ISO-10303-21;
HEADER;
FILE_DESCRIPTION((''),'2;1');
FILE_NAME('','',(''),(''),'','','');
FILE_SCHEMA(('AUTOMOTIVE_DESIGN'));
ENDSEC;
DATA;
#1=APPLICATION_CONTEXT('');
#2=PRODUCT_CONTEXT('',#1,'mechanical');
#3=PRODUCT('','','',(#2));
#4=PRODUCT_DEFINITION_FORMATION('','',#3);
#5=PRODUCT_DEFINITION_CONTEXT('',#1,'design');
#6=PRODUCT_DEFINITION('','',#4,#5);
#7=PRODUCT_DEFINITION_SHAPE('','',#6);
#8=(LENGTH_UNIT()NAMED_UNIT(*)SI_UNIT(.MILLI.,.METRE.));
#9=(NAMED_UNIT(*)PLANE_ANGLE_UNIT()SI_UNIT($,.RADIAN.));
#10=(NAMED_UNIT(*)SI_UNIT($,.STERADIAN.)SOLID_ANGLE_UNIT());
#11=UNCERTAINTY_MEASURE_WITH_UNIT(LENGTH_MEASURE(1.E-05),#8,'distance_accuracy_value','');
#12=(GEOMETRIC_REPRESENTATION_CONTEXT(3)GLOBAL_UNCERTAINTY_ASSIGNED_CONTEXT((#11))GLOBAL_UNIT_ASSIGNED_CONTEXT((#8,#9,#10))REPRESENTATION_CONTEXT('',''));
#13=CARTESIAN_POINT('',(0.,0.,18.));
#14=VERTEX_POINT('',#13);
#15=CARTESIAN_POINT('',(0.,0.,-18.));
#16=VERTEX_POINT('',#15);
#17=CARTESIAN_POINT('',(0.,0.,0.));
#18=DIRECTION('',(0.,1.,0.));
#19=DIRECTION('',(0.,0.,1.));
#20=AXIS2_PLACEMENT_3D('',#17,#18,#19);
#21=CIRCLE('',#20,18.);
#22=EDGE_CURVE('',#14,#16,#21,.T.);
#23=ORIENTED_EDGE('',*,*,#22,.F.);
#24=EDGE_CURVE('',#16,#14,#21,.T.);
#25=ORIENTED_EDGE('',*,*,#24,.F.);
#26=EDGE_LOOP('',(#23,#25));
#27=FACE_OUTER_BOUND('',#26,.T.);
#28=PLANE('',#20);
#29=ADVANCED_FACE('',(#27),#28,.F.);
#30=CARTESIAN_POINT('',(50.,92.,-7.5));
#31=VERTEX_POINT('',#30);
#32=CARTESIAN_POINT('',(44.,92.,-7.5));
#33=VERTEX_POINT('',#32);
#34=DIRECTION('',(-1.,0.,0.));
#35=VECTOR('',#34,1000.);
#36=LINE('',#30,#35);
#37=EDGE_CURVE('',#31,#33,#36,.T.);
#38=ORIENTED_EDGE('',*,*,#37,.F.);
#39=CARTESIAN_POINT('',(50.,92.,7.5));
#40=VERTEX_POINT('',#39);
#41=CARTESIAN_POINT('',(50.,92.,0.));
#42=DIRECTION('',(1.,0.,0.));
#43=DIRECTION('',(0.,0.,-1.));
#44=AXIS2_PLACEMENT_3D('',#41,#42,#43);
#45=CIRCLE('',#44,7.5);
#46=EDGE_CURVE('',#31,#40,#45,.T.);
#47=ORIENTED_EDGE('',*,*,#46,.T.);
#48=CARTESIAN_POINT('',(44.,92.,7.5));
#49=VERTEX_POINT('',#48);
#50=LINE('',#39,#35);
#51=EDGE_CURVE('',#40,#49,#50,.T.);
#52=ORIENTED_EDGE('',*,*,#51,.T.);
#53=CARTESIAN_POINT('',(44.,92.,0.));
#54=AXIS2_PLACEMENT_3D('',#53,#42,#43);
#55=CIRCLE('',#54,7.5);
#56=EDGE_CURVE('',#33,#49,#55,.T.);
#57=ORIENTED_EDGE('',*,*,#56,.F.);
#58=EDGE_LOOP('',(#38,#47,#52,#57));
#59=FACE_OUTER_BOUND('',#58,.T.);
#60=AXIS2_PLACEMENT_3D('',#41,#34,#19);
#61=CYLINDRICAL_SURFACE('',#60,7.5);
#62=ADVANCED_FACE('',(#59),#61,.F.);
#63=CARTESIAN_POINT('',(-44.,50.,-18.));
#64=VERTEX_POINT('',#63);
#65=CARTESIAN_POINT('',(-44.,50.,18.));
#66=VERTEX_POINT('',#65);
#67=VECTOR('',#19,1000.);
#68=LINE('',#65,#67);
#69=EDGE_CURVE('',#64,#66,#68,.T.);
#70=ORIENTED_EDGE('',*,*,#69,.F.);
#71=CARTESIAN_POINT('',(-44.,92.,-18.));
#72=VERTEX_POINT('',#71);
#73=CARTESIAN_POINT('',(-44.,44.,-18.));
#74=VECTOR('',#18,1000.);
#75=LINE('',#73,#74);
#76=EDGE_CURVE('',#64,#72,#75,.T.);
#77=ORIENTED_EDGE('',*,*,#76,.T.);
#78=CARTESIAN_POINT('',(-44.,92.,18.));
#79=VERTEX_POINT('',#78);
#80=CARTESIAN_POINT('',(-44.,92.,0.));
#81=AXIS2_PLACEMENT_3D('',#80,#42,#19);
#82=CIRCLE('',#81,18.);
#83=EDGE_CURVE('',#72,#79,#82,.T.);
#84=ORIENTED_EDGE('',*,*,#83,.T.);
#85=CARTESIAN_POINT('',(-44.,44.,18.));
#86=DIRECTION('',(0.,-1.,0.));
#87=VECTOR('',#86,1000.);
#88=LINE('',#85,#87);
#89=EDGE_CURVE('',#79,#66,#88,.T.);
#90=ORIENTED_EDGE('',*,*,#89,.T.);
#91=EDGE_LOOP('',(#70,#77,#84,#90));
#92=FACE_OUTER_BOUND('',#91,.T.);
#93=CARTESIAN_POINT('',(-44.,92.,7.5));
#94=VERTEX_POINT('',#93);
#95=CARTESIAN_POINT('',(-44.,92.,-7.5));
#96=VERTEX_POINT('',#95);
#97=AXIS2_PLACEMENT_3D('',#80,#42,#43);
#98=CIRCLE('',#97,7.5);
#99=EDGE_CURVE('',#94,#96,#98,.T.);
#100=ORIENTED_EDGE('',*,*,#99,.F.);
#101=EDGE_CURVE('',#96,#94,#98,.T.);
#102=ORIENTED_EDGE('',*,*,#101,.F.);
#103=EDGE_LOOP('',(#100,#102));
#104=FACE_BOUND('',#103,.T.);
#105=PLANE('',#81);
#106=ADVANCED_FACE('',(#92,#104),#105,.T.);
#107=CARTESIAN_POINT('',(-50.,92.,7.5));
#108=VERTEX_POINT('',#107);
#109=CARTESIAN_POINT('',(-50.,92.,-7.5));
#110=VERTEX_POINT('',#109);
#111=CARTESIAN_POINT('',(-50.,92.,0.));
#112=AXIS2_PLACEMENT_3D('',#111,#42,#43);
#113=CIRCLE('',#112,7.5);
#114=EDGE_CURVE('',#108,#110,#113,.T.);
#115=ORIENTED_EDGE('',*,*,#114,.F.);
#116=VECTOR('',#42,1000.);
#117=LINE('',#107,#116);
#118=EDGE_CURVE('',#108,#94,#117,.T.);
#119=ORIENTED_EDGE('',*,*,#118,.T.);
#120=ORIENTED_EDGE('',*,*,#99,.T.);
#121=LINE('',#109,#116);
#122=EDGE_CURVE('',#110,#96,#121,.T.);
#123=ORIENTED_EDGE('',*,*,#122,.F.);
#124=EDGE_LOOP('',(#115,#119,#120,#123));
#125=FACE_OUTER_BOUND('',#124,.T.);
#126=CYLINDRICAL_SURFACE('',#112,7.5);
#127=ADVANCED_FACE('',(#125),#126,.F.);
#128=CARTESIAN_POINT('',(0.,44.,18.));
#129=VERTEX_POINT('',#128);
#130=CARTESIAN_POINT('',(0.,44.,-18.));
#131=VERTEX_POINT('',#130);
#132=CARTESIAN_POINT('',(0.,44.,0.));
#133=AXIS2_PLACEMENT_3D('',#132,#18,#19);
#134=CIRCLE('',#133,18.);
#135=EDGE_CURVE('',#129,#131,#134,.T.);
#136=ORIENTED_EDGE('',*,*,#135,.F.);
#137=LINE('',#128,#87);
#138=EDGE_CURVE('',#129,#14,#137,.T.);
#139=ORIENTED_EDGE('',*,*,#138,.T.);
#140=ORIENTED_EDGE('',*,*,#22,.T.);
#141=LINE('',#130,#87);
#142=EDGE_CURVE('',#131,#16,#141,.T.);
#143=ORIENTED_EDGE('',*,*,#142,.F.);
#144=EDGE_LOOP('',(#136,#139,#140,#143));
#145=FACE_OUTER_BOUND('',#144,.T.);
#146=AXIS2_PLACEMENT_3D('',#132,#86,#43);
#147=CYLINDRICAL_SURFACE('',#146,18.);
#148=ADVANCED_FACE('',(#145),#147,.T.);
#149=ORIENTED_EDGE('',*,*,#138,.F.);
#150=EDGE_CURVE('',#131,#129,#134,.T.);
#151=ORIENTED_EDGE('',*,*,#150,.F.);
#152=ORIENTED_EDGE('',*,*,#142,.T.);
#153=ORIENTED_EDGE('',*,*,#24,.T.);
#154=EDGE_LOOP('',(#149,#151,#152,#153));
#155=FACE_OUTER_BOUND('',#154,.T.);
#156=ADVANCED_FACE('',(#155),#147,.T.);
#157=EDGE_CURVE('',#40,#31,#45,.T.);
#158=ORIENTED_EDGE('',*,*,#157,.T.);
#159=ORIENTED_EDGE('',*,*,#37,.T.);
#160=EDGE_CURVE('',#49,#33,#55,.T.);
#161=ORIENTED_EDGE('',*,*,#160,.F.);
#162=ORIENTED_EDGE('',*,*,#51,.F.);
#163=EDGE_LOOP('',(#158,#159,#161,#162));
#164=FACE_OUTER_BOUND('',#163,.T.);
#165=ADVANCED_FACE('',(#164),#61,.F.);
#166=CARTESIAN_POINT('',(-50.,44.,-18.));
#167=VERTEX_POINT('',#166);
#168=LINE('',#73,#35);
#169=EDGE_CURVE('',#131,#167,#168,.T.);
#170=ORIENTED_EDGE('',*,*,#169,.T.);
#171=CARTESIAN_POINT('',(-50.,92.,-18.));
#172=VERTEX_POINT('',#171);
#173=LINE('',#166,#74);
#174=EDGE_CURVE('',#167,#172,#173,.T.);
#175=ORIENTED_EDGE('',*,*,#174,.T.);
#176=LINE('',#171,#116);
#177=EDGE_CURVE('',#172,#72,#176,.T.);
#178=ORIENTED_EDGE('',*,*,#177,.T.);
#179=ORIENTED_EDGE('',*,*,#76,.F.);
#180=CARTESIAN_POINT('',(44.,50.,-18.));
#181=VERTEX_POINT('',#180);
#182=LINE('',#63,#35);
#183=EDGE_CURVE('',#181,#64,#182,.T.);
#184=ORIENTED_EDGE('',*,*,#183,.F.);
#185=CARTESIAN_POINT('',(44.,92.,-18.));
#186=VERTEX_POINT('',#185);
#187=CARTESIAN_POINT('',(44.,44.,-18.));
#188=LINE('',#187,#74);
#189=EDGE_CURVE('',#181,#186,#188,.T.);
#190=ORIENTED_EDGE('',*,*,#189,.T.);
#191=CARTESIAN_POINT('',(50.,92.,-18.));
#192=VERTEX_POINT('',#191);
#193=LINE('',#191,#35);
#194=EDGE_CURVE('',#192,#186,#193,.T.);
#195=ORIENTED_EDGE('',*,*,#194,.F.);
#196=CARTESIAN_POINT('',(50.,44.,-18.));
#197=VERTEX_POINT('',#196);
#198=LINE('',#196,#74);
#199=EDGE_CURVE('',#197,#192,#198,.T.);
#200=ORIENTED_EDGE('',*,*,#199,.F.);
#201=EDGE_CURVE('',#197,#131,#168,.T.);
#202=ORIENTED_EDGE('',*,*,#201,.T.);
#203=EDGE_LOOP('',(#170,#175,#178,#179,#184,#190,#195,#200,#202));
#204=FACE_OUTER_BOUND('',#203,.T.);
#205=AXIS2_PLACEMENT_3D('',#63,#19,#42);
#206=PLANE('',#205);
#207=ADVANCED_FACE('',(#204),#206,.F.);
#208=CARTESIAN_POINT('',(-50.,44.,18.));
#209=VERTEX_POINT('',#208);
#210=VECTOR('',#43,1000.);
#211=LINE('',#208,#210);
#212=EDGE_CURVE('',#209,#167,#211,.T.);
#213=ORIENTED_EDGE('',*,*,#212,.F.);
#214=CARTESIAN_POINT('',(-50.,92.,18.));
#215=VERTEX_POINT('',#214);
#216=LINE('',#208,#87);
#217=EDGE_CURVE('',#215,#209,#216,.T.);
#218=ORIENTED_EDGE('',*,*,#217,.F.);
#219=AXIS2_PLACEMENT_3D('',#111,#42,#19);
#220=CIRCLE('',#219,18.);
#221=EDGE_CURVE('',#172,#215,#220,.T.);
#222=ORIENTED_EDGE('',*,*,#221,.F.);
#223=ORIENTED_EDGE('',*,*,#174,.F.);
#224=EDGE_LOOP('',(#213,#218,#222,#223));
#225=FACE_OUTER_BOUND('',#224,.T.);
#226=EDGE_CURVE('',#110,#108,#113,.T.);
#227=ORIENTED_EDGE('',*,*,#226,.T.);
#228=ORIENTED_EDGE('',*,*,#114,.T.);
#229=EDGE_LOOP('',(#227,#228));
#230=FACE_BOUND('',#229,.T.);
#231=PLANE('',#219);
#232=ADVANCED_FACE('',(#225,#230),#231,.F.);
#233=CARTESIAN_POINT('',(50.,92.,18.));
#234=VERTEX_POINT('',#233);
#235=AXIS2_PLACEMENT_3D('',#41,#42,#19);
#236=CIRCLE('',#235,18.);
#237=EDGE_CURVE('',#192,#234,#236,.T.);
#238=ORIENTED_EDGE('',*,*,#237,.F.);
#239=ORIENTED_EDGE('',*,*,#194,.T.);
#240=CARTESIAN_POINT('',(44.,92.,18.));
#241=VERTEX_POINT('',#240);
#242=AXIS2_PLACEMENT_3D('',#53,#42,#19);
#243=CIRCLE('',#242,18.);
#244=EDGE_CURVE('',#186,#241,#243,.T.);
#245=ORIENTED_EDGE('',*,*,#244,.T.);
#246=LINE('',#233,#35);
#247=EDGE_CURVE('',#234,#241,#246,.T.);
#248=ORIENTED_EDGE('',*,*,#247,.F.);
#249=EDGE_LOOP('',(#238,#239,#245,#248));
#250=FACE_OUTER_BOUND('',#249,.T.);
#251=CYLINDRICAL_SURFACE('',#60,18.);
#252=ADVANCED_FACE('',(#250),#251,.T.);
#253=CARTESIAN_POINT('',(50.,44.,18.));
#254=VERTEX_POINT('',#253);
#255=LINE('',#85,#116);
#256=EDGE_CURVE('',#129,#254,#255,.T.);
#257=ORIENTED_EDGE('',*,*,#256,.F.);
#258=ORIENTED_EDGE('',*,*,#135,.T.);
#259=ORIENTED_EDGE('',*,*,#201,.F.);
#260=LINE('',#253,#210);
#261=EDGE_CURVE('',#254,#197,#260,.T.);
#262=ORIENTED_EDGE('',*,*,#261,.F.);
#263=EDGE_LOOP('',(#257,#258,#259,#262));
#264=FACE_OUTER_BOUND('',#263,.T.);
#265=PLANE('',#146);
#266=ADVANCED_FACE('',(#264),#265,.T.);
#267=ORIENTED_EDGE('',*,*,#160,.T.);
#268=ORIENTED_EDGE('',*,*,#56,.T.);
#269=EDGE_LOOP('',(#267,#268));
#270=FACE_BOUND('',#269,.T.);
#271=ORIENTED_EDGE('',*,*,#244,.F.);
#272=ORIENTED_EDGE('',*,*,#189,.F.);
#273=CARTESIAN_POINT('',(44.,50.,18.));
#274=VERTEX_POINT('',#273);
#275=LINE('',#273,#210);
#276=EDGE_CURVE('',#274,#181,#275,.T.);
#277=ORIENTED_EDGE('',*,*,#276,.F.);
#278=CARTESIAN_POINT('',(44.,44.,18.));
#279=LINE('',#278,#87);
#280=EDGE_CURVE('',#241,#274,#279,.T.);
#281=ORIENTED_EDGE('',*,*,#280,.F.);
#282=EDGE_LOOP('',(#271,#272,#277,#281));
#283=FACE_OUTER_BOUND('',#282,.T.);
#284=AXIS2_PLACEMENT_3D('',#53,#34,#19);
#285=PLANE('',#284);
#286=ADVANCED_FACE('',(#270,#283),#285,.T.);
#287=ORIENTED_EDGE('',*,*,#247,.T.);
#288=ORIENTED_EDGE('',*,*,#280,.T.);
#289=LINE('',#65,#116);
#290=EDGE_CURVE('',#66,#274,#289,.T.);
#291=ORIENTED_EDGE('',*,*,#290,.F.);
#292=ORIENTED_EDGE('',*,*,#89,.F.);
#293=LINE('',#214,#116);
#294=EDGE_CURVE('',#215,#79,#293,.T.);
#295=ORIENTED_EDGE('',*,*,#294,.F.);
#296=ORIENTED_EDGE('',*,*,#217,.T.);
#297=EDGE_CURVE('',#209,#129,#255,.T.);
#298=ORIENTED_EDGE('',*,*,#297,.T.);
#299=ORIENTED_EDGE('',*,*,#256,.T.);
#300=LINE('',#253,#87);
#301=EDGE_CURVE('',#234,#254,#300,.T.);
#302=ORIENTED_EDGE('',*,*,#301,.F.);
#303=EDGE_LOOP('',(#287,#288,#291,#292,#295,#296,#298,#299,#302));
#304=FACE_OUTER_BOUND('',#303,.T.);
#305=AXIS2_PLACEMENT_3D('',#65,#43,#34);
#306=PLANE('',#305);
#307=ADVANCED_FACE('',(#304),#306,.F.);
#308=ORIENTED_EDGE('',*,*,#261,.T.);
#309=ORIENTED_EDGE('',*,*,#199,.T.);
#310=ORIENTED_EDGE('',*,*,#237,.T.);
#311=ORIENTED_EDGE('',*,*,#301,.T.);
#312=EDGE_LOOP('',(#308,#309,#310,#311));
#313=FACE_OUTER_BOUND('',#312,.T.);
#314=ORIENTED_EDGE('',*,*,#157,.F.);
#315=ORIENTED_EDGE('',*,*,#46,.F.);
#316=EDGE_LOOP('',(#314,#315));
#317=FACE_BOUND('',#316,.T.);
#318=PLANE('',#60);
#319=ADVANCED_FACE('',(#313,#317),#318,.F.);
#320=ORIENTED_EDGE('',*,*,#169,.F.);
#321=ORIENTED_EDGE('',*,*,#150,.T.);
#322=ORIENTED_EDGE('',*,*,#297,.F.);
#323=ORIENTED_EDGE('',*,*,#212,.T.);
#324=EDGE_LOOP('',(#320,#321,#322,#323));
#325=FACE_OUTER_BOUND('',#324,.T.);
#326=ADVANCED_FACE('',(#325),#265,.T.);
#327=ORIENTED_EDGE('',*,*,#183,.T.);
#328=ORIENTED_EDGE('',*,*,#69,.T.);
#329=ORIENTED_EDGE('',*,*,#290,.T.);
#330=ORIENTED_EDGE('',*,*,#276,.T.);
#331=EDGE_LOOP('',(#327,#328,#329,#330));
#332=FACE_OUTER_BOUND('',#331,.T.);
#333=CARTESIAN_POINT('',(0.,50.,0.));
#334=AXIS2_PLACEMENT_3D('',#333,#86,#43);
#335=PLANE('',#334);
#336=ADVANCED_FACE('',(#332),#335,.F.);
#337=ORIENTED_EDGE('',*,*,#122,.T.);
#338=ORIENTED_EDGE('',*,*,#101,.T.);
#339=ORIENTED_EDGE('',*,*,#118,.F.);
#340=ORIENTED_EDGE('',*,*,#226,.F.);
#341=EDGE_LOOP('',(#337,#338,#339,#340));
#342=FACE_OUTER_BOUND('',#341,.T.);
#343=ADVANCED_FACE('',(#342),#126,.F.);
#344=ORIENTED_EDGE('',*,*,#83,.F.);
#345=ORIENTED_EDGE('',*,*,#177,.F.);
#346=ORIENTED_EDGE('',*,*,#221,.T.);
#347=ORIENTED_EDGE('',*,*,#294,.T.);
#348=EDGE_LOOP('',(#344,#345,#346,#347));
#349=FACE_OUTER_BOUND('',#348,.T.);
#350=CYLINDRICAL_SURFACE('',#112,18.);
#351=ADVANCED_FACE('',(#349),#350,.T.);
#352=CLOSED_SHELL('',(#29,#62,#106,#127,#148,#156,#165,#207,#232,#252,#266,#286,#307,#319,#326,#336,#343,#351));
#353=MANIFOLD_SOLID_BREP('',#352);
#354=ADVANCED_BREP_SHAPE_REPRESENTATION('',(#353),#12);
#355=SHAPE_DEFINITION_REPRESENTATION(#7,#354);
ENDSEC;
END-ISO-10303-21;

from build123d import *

# Parameters (mm, degrees)
STEM_PROFILE_36_R           = 18
STEM_36X44_DEPTH            = 44
BASE_PLATE_PROFILE_W        = 88
BASE_PLATE_PROFILE_H        = 36
BASE_PLATE_88X36X6_DEPTH    = 6
LUG_PROFILE_WITH_PIN_HOLE_R = 7.5
LUG_6MM_DEPTH               = 6


with BuildPart() as part:
    # Stem Profile Ø36 → Stem Ø36x44 (new body)
    with BuildSketch(Plane(origin=(0, 0, 0), x_dir=(1, 0, 0), z_dir=(0, 1, 0))):
        with Locations(Location((0, 0, 0), (0, 0, 270))):
            Circle(STEM_PROFILE_36_R)
    extrude(amount=STEM_36X44_DEPTH)

    # Base Plate Profile → Base Plate 88x36x6 (add)
    with BuildSketch(Plane(origin=(0, 44, 0), x_dir=(1, 0, 0), z_dir=(0, 1, 0))):
        Rectangle(BASE_PLATE_PROFILE_W, BASE_PLATE_PROFILE_H)
    extrude(amount=BASE_PLATE_88X36X6_DEPTH)

    # Lug Profile with Pin Hole → Lug 6mm (add)
    with BuildSketch(Plane(origin=(44, 0, 0), x_dir=(0, 0, -1), z_dir=(1, 0, 0))):
        with BuildLine():
            Line((-18, 44), (18, 44))
            Line((18, 44), (18, 92))
            ThreePointArc((18, 92), (0, 110), (-18, 92))
            Line((-18, 92), (-18, 44))
        make_face()
        with Locations((0, 92)):
            Circle(LUG_PROFILE_WITH_PIN_HOLE_R, mode=Mode.SUBTRACT)
    lug_6mm = extrude(amount=LUG_6MM_DEPTH)

    # Lug Mirror: Lug 6mm across plane
    add(lug_6mm.mirror(Plane(origin=(0, 0, 0), x_dir=(0, 0, 1), z_dir=(1, 0, 0))))


solid = part.part
